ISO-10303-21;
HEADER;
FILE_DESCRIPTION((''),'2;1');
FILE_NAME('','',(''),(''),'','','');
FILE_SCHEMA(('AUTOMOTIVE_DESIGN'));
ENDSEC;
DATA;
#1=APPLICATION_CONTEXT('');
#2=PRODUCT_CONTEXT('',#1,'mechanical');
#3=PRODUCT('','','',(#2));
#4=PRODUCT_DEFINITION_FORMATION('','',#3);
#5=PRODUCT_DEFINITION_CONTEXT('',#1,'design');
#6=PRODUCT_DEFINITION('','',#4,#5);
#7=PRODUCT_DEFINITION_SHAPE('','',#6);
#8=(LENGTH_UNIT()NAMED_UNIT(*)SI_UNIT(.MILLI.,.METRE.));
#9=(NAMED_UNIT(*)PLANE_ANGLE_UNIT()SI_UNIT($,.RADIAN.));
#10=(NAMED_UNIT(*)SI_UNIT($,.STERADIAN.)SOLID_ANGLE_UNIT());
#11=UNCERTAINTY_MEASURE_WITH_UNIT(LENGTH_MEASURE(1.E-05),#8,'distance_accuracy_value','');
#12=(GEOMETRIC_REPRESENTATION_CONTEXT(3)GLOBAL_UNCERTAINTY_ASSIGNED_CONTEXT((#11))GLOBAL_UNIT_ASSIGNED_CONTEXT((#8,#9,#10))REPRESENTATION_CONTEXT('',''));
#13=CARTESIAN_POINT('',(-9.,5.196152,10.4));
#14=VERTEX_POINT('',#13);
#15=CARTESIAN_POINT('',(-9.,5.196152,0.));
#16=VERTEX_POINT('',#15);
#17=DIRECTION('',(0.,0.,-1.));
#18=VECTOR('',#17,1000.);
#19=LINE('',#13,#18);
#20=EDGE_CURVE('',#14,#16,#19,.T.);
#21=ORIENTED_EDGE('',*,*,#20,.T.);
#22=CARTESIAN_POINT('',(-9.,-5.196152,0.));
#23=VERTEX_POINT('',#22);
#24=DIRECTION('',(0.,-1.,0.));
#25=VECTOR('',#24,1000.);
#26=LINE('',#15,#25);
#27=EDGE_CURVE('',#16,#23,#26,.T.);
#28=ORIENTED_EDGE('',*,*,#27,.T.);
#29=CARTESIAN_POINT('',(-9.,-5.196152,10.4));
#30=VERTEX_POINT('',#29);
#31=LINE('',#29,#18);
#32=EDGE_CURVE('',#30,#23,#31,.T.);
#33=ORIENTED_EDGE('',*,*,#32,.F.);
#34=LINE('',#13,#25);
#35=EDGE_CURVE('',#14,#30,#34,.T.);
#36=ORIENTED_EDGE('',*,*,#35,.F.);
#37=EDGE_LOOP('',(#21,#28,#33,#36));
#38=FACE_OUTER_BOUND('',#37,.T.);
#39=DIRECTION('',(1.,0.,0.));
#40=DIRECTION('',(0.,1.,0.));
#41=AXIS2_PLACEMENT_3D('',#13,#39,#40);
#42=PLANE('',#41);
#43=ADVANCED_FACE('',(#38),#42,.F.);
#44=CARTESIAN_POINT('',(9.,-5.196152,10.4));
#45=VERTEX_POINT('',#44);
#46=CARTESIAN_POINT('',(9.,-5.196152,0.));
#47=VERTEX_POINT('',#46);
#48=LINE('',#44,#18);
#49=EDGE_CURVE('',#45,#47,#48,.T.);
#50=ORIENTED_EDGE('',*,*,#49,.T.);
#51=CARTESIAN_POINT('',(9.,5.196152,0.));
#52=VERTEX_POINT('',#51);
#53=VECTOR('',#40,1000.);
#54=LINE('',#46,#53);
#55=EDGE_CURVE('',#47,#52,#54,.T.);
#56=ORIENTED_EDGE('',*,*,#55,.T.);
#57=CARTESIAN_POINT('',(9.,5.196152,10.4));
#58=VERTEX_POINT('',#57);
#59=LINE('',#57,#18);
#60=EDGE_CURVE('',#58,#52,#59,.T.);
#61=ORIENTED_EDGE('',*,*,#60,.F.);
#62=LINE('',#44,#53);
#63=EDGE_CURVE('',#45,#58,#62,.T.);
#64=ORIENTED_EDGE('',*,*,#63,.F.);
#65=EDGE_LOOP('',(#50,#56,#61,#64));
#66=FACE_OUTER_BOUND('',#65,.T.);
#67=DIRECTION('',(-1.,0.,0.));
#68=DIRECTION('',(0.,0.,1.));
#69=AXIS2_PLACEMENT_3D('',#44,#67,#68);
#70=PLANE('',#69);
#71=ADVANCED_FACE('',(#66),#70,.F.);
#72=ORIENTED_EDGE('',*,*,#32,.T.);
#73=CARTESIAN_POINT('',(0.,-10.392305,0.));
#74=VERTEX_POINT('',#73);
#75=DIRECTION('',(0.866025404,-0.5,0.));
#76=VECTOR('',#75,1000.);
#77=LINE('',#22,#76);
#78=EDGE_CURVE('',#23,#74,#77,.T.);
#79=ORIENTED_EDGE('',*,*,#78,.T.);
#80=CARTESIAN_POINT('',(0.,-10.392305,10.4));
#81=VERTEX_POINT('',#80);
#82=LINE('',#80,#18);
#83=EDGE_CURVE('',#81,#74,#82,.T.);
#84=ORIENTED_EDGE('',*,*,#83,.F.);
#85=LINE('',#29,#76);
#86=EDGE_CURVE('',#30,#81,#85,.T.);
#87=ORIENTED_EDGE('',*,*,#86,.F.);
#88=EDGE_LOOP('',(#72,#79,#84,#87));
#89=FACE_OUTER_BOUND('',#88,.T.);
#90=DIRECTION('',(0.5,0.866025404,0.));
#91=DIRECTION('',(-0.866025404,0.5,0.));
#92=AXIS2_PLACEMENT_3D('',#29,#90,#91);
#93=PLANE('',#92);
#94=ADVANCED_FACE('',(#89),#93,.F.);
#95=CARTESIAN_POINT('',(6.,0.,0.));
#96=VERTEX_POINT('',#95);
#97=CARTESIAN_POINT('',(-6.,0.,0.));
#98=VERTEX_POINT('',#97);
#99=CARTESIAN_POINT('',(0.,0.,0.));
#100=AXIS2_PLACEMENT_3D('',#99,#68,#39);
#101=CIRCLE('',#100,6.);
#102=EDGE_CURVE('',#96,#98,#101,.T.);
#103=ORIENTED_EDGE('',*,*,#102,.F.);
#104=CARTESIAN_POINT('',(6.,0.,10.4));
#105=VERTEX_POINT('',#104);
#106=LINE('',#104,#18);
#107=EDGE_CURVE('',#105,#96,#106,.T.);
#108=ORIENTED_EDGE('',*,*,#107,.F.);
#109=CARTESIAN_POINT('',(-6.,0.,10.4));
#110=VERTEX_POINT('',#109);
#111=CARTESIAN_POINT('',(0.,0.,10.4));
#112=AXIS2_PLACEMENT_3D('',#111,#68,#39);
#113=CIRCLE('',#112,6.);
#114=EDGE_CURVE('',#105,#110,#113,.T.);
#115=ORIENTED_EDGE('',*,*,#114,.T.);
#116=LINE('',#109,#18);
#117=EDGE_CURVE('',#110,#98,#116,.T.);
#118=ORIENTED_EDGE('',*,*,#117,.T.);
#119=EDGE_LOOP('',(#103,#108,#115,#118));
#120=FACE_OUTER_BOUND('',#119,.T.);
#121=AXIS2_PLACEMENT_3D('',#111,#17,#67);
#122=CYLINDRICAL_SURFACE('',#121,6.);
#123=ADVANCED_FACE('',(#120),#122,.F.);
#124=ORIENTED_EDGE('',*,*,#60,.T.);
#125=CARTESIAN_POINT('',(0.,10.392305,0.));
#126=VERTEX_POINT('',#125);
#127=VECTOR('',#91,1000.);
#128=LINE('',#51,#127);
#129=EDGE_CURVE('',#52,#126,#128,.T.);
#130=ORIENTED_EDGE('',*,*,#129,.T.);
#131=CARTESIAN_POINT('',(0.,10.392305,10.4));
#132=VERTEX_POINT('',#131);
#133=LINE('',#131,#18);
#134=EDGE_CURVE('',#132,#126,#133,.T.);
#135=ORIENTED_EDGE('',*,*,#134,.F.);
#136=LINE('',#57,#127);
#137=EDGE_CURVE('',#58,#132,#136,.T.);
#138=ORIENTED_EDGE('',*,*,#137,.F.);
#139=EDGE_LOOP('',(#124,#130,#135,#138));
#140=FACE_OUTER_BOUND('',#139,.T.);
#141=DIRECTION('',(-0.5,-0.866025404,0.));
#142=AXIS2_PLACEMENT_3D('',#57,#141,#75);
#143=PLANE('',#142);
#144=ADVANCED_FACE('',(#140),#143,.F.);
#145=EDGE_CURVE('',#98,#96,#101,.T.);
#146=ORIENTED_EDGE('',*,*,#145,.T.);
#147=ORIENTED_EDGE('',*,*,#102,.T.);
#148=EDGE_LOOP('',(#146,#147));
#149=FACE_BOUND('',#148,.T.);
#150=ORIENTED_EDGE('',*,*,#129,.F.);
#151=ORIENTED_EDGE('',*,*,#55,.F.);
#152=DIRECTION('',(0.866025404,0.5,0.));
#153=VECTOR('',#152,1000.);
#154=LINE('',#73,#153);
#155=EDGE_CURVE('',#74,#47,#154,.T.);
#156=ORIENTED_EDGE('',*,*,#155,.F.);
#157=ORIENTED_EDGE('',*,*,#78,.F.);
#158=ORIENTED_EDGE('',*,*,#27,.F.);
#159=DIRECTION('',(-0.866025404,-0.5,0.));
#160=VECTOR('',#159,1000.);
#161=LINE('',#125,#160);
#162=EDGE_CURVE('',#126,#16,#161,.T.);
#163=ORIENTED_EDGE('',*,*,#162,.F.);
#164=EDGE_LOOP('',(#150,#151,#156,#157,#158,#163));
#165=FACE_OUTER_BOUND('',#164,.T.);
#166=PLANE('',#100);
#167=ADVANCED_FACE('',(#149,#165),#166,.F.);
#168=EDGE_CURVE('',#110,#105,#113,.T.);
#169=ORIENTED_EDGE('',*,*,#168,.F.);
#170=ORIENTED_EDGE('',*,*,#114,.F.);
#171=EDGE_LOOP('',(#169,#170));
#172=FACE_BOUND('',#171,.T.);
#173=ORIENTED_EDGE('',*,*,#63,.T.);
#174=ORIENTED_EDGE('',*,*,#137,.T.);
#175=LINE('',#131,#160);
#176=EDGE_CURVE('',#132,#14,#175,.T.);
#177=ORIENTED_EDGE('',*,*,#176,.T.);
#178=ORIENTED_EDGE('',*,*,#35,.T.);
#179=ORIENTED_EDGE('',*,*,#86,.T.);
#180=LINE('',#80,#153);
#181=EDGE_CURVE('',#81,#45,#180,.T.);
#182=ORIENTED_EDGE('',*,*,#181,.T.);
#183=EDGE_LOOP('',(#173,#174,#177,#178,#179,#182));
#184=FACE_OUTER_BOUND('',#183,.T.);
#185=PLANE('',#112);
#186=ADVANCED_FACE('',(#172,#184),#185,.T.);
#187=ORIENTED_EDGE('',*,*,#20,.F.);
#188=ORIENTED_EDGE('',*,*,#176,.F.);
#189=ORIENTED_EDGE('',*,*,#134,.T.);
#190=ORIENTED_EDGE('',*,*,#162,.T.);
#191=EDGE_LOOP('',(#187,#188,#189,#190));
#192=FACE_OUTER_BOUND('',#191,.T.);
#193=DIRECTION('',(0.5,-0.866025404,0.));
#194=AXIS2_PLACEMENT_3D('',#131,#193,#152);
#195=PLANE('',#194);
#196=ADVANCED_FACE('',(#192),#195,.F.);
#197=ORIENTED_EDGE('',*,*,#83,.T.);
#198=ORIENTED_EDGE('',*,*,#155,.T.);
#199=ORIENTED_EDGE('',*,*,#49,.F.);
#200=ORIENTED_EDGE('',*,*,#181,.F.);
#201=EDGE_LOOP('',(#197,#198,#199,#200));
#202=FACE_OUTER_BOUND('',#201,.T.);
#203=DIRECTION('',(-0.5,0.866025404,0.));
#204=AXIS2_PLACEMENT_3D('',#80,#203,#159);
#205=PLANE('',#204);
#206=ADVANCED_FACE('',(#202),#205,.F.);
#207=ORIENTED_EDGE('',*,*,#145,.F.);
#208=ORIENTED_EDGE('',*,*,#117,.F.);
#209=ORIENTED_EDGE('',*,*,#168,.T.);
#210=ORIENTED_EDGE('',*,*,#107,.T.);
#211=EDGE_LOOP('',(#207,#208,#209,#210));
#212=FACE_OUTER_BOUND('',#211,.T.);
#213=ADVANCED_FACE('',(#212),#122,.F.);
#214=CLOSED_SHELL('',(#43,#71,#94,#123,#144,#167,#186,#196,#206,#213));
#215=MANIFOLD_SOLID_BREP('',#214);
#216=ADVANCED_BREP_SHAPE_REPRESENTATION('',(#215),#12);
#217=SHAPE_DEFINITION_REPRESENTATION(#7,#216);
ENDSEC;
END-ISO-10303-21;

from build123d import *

# Parameters (mm, degrees)
SKETCH1_R           = 6
BOSS_EXTRUDE1_DEPTH = 10.4


with BuildPart() as part:
    # Sketch1 → Boss-Extrude1 (new body)
    with BuildSketch(Plane.XY):
        Polygon((0, -10.392304845), (9, -5.196152423), (9, 5.196152423), (0, 10.392304845), (-9, 5.196152423), (-9, -5.196152423), align=None)
        Circle(SKETCH1_R, mode=Mode.SUBTRACT)
    extrude(amount=BOSS_EXTRUDE1_DEPTH)


solid = part.part
